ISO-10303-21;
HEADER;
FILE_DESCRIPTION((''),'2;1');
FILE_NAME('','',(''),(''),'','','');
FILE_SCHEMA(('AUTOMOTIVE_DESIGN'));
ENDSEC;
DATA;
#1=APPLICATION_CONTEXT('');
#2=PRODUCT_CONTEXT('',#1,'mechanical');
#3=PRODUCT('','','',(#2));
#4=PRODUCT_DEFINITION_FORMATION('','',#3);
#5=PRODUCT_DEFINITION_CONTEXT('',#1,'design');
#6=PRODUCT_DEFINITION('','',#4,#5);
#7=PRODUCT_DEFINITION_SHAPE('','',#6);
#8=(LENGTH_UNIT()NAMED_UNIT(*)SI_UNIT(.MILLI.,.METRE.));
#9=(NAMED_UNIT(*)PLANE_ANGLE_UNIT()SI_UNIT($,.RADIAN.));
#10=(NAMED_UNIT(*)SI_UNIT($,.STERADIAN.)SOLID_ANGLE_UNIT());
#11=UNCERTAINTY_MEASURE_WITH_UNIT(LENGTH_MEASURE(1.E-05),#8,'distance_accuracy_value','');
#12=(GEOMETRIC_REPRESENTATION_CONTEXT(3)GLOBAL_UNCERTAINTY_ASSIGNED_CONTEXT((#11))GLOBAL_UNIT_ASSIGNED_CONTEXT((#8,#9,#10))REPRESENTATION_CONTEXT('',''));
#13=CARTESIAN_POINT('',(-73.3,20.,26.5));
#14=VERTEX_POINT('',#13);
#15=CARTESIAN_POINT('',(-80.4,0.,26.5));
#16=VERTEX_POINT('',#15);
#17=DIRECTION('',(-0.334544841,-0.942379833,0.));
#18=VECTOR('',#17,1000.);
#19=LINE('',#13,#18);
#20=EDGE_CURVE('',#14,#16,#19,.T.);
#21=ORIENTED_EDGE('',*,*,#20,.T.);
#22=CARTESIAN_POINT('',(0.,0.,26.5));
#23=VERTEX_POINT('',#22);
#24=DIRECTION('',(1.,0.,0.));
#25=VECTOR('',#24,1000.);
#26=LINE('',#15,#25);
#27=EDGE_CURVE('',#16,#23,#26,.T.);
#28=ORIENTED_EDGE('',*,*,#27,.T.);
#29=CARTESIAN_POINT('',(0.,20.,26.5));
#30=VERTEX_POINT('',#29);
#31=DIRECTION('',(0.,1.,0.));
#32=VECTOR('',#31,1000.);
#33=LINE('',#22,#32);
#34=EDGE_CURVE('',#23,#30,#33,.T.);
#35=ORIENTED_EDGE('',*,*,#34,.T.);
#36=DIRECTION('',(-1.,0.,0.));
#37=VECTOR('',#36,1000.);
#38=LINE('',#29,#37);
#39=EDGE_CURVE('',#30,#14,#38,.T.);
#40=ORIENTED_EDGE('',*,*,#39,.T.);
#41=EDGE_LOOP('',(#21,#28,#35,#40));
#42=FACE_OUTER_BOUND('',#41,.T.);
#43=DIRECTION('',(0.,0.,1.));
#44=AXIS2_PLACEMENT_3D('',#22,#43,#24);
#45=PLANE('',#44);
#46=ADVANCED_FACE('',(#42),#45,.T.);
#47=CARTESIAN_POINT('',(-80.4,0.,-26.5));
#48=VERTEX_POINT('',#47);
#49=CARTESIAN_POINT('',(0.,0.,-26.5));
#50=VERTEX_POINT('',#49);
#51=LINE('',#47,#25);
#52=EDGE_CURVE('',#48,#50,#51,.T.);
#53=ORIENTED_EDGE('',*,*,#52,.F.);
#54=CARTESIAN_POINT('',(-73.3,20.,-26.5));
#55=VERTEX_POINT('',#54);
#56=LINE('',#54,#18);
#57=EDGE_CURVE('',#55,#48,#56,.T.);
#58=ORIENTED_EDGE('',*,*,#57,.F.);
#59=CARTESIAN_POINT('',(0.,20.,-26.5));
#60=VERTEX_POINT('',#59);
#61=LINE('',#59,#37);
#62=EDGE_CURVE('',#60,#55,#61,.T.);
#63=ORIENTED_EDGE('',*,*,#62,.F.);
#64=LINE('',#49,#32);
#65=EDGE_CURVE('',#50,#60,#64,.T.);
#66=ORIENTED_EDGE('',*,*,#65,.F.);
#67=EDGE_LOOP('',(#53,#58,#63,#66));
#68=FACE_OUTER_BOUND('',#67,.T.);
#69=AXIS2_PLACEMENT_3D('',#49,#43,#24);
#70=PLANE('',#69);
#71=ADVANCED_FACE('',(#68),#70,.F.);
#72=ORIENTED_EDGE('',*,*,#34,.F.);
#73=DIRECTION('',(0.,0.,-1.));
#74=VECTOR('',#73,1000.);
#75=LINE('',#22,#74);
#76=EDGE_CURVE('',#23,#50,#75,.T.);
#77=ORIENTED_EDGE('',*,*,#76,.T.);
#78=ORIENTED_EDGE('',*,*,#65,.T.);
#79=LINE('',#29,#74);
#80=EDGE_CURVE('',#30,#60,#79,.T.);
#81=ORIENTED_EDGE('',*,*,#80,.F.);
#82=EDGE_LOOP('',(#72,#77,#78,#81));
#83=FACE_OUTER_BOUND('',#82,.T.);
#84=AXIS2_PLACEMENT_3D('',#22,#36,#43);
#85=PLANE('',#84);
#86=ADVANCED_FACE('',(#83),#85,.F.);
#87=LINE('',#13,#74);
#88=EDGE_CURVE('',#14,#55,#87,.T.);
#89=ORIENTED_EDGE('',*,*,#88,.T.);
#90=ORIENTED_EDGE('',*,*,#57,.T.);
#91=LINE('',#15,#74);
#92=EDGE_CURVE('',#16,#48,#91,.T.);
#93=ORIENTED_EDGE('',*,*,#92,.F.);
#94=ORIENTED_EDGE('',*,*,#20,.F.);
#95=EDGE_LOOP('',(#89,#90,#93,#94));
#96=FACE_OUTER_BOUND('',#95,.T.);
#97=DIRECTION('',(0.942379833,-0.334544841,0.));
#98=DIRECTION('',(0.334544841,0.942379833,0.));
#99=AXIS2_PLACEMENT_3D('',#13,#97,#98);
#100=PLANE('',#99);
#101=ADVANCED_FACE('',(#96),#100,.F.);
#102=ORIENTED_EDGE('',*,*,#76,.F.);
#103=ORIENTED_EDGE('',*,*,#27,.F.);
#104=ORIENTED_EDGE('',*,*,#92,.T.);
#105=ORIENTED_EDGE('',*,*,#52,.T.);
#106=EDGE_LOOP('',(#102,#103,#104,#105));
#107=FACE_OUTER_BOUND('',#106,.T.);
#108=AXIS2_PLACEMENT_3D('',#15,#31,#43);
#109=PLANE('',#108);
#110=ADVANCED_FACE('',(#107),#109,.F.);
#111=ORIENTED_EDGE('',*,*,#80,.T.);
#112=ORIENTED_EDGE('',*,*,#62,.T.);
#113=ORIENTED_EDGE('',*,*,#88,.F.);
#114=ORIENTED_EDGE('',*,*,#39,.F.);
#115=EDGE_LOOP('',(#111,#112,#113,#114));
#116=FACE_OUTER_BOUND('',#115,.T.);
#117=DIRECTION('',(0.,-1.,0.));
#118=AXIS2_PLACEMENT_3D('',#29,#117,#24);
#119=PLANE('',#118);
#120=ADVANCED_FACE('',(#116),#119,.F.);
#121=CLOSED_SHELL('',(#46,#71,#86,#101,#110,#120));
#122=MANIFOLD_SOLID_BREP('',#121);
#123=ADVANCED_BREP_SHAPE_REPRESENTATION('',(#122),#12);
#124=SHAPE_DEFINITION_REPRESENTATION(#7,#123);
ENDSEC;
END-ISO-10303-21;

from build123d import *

# Parameters (mm, degrees)
EXTRUDE_1_DEPTH = 26.5


with BuildPart() as part:
    # 草图1 → 凸台-拉伸1 (new, symmetric)
    with BuildSketch(Plane.XY):
        Polygon((0, 0), (0, 20), (-73.3, 20), (-80.4, 0), align=None)
    extrude(amount=EXTRUDE_1_DEPTH, both=True)


solid = part.part
